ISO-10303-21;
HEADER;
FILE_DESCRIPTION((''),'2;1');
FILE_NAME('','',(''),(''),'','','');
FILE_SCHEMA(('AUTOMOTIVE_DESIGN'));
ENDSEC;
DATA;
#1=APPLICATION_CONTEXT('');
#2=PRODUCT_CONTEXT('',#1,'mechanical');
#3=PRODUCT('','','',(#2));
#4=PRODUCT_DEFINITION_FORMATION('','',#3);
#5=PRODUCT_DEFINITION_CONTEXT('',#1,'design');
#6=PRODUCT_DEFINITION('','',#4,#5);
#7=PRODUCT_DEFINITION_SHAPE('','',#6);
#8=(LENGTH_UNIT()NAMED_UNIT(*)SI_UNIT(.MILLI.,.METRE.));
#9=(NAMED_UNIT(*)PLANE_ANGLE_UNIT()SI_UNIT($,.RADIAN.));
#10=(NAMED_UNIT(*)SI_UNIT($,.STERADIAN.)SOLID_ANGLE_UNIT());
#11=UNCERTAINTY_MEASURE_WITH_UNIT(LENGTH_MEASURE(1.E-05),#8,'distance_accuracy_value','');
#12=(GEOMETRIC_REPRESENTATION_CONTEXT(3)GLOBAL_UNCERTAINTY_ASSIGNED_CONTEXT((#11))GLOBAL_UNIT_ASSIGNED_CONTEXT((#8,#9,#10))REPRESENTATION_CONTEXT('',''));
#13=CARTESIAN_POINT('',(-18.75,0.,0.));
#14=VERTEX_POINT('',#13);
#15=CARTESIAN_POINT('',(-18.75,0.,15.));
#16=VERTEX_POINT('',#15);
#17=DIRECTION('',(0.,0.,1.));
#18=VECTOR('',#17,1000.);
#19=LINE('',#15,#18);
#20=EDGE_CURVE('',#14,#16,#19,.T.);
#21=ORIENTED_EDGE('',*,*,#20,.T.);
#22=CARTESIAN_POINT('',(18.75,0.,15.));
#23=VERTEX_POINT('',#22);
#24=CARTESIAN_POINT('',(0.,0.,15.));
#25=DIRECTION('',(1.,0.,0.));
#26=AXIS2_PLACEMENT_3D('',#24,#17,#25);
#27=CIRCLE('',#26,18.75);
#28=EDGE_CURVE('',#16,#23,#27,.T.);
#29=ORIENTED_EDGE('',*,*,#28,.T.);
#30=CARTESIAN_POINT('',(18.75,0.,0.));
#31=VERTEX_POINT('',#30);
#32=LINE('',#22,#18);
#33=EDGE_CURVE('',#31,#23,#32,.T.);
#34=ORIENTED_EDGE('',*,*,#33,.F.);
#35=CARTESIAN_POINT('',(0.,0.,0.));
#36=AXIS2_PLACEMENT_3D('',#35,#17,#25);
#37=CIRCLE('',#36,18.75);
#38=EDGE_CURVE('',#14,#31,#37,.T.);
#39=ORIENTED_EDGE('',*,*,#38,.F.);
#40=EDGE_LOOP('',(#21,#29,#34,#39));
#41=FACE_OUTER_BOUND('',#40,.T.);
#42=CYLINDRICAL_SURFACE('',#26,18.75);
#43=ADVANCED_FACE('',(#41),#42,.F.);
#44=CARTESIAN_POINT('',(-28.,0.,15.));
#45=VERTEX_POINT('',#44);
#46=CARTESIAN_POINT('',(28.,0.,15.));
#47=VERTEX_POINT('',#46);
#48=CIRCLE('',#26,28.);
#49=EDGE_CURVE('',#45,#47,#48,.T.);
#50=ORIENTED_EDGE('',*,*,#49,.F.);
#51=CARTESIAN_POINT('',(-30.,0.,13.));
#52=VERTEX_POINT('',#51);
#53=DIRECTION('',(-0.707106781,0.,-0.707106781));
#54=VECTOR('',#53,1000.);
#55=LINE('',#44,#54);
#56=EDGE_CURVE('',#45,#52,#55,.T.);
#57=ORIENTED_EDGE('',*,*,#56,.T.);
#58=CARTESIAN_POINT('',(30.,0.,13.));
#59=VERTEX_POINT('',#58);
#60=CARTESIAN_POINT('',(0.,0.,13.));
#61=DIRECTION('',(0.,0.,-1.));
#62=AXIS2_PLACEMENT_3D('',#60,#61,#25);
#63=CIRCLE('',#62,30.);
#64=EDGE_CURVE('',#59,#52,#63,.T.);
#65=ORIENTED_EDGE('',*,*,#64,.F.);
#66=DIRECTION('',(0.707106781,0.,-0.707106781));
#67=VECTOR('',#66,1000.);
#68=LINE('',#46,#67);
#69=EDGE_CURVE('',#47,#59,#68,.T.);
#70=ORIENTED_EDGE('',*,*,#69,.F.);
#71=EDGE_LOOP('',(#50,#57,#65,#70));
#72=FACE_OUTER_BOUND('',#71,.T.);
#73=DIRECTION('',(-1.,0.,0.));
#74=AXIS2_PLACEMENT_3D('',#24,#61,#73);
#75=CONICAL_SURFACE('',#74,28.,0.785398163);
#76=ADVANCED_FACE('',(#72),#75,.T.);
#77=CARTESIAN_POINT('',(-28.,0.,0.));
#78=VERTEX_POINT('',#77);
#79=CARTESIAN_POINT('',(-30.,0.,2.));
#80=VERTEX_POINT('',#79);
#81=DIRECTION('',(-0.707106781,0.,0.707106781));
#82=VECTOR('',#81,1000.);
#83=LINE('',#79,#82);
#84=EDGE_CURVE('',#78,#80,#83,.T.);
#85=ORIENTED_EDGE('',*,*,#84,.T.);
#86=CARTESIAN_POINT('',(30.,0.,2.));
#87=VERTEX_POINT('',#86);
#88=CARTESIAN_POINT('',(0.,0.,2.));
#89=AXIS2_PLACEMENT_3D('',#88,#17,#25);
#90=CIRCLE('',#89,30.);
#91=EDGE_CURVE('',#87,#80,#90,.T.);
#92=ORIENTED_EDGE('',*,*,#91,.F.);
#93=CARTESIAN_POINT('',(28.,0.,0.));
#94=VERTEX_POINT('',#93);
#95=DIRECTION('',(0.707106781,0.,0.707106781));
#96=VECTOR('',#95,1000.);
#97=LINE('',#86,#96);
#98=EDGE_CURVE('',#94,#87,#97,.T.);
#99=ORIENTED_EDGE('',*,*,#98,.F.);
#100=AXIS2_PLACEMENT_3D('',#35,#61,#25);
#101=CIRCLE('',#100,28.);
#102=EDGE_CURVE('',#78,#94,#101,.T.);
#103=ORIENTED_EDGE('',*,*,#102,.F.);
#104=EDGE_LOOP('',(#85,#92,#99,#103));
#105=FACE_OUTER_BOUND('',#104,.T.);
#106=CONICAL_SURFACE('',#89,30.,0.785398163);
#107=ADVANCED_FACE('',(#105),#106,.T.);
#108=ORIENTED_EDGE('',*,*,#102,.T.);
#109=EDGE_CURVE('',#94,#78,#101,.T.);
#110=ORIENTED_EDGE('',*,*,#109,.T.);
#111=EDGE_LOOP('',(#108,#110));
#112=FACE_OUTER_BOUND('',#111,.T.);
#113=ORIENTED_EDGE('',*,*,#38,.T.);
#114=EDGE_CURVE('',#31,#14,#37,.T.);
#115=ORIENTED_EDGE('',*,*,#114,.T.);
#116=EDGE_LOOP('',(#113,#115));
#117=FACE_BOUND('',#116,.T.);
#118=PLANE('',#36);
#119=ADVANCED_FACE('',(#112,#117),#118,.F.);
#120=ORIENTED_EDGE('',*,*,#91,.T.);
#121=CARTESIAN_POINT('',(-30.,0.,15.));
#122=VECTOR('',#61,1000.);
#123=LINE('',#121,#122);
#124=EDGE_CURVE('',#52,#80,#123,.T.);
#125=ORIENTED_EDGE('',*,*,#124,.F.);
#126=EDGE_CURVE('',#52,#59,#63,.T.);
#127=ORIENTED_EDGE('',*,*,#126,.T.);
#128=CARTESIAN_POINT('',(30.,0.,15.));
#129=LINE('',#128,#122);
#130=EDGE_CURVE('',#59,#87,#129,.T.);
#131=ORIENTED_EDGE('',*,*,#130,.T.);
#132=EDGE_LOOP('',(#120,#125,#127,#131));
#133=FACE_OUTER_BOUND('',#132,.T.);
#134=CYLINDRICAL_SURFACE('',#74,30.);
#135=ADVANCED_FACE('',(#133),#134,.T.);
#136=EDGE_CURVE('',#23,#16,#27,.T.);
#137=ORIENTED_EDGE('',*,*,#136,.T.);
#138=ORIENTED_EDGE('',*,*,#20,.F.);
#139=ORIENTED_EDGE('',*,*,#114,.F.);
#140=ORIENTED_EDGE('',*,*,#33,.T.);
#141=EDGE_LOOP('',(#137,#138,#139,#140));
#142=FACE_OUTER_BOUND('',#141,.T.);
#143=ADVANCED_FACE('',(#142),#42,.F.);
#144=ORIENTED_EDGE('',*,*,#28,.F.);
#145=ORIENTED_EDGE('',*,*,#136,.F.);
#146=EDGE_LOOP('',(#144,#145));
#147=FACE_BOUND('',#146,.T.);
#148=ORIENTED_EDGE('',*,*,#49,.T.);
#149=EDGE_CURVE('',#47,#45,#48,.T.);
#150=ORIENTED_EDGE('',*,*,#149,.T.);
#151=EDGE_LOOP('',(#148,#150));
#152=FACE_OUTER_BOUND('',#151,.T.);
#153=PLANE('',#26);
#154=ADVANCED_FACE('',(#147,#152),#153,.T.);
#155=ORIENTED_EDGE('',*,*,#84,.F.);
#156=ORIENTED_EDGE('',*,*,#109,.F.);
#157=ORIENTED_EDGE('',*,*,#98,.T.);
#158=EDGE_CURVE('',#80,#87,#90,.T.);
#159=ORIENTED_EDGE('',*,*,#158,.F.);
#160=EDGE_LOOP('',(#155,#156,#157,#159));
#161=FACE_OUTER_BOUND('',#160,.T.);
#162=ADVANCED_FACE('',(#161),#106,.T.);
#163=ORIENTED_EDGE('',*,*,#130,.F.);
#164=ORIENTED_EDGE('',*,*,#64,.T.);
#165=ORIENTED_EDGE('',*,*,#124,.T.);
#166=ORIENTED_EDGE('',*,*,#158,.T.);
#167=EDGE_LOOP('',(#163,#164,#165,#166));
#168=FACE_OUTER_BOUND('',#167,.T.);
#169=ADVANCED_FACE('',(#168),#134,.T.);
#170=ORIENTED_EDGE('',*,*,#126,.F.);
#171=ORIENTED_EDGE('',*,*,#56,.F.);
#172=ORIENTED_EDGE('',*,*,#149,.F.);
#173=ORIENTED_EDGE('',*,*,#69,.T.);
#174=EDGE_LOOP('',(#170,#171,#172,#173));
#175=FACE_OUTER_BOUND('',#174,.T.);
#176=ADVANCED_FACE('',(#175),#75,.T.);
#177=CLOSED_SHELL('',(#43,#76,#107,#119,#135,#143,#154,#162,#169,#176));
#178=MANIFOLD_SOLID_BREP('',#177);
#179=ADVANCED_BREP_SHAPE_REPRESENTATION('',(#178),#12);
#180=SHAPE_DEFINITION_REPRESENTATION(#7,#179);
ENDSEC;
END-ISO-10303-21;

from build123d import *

# Parameters (mm, degrees)
SKETCH1_R              = 30
BOSS_EXTRUDE1_DEPTH    = 15
SKETCH2_R              = 17.5
CUT_EXTRUDE1_DEPTH     = 15
CHAMFER1_SIZE          = 2
M42_TAPPED_HOLE2_D     = 37.5
M42_TAPPED_HOLE2_DEPTH = 106.5
M42_TAPPED_HOLE2_TIP   = 11.266136607


with BuildPart() as part:
    # Sketch1 → Boss-Extrude1 (new body)
    with BuildSketch(Plane.XY):
        Circle(SKETCH1_R)
    extrude(amount=BOSS_EXTRUDE1_DEPTH)

    # Sketch2 → Cut-Extrude1 (cut)
    with BuildSketch(Plane.XY.offset(15)):
        Circle(SKETCH2_R)
    extrude(amount=-CUT_EXTRUDE1_DEPTH, mode=Mode.SUBTRACT)

    # Chamfer1
    chamfer1_edges = [part.edges().sort_by_distance(p)[0] for p in [
        (-30, 0, 0),
        (-30, 0, 15),
    ]]
    chamfer(chamfer1_edges, length=CHAMFER1_SIZE)

    # M42 Tapped Hole2
    with Locations(Plane.XY.offset(15)):
        with Locations((0, 0)):
            Hole(M42_TAPPED_HOLE2_D / 2, depth=M42_TAPPED_HOLE2_DEPTH)
            with Locations((0, 0, -(M42_TAPPED_HOLE2_DEPTH + M42_TAPPED_HOLE2_TIP / 2))):  # 118° drill point
                Cone(0, M42_TAPPED_HOLE2_D / 2, M42_TAPPED_HOLE2_TIP, mode=Mode.SUBTRACT)


solid = part.part
